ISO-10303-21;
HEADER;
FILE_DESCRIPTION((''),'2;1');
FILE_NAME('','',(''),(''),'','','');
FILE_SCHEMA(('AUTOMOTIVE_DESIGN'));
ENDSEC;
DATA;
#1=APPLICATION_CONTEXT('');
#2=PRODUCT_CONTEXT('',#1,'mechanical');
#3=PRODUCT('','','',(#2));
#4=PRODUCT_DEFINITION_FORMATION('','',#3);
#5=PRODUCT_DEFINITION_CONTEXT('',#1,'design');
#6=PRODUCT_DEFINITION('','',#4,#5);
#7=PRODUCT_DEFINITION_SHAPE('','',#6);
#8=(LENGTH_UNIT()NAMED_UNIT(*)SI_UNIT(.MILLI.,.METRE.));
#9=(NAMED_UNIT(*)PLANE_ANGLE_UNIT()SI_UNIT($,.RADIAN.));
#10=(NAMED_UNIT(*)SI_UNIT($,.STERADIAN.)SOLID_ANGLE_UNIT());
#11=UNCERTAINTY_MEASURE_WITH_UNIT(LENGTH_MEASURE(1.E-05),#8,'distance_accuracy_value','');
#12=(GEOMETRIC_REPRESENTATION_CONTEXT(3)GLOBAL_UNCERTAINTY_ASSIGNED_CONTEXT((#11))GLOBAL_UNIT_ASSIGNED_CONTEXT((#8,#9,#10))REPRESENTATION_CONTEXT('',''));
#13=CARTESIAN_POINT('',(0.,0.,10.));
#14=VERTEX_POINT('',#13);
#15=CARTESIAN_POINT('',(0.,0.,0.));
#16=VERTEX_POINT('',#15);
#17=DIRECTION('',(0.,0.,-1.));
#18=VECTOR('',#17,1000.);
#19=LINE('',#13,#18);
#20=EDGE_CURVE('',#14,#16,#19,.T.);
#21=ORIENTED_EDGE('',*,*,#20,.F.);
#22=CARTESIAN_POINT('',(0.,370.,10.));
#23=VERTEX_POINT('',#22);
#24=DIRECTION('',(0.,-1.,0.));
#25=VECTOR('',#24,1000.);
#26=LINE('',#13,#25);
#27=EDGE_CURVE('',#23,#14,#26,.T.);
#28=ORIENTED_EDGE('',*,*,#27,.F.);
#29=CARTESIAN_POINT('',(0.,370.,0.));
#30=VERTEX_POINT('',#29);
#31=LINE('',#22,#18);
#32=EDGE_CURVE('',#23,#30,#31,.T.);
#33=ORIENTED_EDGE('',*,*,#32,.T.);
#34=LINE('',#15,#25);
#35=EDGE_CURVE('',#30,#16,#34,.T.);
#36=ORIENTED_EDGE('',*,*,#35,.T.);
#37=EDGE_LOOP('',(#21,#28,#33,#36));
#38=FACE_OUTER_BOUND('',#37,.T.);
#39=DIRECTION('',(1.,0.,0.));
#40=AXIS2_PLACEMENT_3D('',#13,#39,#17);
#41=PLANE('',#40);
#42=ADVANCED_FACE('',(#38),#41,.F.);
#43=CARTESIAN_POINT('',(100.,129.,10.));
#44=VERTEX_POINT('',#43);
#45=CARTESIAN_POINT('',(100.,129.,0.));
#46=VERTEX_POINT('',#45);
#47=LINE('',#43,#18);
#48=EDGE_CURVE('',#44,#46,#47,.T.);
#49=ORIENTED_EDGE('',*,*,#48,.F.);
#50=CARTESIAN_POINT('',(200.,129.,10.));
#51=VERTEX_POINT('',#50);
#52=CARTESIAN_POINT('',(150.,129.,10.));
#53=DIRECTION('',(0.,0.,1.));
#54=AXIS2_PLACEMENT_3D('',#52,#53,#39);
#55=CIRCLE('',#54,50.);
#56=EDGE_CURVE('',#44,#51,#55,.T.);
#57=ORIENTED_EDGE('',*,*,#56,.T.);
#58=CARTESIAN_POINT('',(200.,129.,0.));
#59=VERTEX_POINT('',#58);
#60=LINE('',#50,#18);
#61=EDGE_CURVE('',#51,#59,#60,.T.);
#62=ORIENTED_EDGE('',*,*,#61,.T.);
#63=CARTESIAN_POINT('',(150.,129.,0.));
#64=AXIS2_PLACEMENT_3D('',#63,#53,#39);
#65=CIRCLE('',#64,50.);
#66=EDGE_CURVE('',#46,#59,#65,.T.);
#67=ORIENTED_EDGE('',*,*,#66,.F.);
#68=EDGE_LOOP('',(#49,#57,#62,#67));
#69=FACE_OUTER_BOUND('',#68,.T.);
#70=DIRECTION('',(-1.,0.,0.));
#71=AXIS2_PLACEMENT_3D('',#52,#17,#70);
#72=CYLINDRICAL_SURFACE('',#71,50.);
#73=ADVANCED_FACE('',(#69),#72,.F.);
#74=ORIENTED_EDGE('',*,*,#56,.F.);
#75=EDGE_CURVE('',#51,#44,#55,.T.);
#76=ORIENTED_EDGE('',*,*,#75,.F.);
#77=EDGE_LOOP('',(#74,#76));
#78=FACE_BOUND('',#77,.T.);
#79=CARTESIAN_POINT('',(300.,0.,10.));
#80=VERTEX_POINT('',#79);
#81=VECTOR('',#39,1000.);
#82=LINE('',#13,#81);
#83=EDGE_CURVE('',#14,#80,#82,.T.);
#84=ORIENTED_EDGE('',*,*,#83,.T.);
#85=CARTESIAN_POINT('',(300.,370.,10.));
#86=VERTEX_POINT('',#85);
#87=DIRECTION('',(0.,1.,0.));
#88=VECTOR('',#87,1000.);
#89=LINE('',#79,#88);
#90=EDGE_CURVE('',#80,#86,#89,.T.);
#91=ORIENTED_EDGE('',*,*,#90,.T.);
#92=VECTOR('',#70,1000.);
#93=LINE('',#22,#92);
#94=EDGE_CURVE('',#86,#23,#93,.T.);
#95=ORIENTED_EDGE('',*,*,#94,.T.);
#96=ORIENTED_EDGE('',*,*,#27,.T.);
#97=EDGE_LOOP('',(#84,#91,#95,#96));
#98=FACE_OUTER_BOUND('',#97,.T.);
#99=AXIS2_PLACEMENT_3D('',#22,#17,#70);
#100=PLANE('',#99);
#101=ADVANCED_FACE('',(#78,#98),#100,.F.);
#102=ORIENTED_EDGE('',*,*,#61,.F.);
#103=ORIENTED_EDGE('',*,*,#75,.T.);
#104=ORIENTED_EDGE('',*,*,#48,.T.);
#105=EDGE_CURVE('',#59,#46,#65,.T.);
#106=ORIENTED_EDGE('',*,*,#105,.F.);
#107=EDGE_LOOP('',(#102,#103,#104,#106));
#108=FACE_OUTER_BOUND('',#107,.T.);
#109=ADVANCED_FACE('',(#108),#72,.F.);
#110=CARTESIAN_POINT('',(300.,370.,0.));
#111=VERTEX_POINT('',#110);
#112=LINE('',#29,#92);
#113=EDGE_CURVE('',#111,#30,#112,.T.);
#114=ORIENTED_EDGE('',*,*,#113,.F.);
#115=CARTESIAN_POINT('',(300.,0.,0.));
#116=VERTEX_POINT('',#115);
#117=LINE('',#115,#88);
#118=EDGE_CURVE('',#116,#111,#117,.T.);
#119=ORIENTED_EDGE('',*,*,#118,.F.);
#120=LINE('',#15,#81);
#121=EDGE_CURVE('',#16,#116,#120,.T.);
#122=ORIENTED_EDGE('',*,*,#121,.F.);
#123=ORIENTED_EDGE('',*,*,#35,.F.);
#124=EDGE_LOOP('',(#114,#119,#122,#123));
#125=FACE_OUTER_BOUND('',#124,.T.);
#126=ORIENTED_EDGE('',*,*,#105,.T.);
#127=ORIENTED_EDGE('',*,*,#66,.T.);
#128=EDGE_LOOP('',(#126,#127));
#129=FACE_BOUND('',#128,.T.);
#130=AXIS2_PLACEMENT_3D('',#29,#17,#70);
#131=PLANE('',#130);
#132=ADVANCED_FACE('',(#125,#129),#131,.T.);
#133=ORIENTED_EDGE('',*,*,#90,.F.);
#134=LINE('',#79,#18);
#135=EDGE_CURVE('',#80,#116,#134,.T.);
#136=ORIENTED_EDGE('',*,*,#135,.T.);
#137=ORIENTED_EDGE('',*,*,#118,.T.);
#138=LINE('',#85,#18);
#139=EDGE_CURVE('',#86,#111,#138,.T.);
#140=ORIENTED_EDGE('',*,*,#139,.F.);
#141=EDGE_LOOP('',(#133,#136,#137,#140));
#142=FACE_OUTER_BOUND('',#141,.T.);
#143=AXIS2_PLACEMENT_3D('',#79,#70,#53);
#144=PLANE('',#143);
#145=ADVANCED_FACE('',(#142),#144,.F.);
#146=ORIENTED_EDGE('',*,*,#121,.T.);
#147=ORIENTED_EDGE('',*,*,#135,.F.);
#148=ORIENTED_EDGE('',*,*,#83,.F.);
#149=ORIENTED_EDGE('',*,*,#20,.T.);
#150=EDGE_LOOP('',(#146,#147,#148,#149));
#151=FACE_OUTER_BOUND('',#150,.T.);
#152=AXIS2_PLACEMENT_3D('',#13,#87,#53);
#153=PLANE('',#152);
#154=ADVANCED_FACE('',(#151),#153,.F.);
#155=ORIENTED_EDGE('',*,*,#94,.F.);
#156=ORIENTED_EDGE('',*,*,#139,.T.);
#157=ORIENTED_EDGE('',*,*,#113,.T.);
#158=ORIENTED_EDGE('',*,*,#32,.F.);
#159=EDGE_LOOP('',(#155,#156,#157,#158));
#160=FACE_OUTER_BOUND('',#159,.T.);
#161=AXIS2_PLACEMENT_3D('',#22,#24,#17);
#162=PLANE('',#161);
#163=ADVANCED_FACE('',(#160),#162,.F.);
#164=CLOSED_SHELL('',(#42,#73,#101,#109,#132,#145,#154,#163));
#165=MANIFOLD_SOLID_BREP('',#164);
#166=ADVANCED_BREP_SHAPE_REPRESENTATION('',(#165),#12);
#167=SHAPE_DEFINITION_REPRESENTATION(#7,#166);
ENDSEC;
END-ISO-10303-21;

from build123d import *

# Parameters (mm, degrees)
SKETCH1_W           = 300
SKETCH1_H           = 370
SKETCH1_R           = 50
BOSS_EXTRUDE1_DEPTH = 10


with BuildPart() as part:
    # Sketch1 → Boss-Extrude1 (new body)
    with BuildSketch(Plane.XY):
        with Locations((150, 185)):
            Rectangle(SKETCH1_W, SKETCH1_H)
        with Locations((150, 129)):
            Circle(SKETCH1_R, mode=Mode.SUBTRACT)
    extrude(amount=BOSS_EXTRUDE1_DEPTH)


solid = part.part
